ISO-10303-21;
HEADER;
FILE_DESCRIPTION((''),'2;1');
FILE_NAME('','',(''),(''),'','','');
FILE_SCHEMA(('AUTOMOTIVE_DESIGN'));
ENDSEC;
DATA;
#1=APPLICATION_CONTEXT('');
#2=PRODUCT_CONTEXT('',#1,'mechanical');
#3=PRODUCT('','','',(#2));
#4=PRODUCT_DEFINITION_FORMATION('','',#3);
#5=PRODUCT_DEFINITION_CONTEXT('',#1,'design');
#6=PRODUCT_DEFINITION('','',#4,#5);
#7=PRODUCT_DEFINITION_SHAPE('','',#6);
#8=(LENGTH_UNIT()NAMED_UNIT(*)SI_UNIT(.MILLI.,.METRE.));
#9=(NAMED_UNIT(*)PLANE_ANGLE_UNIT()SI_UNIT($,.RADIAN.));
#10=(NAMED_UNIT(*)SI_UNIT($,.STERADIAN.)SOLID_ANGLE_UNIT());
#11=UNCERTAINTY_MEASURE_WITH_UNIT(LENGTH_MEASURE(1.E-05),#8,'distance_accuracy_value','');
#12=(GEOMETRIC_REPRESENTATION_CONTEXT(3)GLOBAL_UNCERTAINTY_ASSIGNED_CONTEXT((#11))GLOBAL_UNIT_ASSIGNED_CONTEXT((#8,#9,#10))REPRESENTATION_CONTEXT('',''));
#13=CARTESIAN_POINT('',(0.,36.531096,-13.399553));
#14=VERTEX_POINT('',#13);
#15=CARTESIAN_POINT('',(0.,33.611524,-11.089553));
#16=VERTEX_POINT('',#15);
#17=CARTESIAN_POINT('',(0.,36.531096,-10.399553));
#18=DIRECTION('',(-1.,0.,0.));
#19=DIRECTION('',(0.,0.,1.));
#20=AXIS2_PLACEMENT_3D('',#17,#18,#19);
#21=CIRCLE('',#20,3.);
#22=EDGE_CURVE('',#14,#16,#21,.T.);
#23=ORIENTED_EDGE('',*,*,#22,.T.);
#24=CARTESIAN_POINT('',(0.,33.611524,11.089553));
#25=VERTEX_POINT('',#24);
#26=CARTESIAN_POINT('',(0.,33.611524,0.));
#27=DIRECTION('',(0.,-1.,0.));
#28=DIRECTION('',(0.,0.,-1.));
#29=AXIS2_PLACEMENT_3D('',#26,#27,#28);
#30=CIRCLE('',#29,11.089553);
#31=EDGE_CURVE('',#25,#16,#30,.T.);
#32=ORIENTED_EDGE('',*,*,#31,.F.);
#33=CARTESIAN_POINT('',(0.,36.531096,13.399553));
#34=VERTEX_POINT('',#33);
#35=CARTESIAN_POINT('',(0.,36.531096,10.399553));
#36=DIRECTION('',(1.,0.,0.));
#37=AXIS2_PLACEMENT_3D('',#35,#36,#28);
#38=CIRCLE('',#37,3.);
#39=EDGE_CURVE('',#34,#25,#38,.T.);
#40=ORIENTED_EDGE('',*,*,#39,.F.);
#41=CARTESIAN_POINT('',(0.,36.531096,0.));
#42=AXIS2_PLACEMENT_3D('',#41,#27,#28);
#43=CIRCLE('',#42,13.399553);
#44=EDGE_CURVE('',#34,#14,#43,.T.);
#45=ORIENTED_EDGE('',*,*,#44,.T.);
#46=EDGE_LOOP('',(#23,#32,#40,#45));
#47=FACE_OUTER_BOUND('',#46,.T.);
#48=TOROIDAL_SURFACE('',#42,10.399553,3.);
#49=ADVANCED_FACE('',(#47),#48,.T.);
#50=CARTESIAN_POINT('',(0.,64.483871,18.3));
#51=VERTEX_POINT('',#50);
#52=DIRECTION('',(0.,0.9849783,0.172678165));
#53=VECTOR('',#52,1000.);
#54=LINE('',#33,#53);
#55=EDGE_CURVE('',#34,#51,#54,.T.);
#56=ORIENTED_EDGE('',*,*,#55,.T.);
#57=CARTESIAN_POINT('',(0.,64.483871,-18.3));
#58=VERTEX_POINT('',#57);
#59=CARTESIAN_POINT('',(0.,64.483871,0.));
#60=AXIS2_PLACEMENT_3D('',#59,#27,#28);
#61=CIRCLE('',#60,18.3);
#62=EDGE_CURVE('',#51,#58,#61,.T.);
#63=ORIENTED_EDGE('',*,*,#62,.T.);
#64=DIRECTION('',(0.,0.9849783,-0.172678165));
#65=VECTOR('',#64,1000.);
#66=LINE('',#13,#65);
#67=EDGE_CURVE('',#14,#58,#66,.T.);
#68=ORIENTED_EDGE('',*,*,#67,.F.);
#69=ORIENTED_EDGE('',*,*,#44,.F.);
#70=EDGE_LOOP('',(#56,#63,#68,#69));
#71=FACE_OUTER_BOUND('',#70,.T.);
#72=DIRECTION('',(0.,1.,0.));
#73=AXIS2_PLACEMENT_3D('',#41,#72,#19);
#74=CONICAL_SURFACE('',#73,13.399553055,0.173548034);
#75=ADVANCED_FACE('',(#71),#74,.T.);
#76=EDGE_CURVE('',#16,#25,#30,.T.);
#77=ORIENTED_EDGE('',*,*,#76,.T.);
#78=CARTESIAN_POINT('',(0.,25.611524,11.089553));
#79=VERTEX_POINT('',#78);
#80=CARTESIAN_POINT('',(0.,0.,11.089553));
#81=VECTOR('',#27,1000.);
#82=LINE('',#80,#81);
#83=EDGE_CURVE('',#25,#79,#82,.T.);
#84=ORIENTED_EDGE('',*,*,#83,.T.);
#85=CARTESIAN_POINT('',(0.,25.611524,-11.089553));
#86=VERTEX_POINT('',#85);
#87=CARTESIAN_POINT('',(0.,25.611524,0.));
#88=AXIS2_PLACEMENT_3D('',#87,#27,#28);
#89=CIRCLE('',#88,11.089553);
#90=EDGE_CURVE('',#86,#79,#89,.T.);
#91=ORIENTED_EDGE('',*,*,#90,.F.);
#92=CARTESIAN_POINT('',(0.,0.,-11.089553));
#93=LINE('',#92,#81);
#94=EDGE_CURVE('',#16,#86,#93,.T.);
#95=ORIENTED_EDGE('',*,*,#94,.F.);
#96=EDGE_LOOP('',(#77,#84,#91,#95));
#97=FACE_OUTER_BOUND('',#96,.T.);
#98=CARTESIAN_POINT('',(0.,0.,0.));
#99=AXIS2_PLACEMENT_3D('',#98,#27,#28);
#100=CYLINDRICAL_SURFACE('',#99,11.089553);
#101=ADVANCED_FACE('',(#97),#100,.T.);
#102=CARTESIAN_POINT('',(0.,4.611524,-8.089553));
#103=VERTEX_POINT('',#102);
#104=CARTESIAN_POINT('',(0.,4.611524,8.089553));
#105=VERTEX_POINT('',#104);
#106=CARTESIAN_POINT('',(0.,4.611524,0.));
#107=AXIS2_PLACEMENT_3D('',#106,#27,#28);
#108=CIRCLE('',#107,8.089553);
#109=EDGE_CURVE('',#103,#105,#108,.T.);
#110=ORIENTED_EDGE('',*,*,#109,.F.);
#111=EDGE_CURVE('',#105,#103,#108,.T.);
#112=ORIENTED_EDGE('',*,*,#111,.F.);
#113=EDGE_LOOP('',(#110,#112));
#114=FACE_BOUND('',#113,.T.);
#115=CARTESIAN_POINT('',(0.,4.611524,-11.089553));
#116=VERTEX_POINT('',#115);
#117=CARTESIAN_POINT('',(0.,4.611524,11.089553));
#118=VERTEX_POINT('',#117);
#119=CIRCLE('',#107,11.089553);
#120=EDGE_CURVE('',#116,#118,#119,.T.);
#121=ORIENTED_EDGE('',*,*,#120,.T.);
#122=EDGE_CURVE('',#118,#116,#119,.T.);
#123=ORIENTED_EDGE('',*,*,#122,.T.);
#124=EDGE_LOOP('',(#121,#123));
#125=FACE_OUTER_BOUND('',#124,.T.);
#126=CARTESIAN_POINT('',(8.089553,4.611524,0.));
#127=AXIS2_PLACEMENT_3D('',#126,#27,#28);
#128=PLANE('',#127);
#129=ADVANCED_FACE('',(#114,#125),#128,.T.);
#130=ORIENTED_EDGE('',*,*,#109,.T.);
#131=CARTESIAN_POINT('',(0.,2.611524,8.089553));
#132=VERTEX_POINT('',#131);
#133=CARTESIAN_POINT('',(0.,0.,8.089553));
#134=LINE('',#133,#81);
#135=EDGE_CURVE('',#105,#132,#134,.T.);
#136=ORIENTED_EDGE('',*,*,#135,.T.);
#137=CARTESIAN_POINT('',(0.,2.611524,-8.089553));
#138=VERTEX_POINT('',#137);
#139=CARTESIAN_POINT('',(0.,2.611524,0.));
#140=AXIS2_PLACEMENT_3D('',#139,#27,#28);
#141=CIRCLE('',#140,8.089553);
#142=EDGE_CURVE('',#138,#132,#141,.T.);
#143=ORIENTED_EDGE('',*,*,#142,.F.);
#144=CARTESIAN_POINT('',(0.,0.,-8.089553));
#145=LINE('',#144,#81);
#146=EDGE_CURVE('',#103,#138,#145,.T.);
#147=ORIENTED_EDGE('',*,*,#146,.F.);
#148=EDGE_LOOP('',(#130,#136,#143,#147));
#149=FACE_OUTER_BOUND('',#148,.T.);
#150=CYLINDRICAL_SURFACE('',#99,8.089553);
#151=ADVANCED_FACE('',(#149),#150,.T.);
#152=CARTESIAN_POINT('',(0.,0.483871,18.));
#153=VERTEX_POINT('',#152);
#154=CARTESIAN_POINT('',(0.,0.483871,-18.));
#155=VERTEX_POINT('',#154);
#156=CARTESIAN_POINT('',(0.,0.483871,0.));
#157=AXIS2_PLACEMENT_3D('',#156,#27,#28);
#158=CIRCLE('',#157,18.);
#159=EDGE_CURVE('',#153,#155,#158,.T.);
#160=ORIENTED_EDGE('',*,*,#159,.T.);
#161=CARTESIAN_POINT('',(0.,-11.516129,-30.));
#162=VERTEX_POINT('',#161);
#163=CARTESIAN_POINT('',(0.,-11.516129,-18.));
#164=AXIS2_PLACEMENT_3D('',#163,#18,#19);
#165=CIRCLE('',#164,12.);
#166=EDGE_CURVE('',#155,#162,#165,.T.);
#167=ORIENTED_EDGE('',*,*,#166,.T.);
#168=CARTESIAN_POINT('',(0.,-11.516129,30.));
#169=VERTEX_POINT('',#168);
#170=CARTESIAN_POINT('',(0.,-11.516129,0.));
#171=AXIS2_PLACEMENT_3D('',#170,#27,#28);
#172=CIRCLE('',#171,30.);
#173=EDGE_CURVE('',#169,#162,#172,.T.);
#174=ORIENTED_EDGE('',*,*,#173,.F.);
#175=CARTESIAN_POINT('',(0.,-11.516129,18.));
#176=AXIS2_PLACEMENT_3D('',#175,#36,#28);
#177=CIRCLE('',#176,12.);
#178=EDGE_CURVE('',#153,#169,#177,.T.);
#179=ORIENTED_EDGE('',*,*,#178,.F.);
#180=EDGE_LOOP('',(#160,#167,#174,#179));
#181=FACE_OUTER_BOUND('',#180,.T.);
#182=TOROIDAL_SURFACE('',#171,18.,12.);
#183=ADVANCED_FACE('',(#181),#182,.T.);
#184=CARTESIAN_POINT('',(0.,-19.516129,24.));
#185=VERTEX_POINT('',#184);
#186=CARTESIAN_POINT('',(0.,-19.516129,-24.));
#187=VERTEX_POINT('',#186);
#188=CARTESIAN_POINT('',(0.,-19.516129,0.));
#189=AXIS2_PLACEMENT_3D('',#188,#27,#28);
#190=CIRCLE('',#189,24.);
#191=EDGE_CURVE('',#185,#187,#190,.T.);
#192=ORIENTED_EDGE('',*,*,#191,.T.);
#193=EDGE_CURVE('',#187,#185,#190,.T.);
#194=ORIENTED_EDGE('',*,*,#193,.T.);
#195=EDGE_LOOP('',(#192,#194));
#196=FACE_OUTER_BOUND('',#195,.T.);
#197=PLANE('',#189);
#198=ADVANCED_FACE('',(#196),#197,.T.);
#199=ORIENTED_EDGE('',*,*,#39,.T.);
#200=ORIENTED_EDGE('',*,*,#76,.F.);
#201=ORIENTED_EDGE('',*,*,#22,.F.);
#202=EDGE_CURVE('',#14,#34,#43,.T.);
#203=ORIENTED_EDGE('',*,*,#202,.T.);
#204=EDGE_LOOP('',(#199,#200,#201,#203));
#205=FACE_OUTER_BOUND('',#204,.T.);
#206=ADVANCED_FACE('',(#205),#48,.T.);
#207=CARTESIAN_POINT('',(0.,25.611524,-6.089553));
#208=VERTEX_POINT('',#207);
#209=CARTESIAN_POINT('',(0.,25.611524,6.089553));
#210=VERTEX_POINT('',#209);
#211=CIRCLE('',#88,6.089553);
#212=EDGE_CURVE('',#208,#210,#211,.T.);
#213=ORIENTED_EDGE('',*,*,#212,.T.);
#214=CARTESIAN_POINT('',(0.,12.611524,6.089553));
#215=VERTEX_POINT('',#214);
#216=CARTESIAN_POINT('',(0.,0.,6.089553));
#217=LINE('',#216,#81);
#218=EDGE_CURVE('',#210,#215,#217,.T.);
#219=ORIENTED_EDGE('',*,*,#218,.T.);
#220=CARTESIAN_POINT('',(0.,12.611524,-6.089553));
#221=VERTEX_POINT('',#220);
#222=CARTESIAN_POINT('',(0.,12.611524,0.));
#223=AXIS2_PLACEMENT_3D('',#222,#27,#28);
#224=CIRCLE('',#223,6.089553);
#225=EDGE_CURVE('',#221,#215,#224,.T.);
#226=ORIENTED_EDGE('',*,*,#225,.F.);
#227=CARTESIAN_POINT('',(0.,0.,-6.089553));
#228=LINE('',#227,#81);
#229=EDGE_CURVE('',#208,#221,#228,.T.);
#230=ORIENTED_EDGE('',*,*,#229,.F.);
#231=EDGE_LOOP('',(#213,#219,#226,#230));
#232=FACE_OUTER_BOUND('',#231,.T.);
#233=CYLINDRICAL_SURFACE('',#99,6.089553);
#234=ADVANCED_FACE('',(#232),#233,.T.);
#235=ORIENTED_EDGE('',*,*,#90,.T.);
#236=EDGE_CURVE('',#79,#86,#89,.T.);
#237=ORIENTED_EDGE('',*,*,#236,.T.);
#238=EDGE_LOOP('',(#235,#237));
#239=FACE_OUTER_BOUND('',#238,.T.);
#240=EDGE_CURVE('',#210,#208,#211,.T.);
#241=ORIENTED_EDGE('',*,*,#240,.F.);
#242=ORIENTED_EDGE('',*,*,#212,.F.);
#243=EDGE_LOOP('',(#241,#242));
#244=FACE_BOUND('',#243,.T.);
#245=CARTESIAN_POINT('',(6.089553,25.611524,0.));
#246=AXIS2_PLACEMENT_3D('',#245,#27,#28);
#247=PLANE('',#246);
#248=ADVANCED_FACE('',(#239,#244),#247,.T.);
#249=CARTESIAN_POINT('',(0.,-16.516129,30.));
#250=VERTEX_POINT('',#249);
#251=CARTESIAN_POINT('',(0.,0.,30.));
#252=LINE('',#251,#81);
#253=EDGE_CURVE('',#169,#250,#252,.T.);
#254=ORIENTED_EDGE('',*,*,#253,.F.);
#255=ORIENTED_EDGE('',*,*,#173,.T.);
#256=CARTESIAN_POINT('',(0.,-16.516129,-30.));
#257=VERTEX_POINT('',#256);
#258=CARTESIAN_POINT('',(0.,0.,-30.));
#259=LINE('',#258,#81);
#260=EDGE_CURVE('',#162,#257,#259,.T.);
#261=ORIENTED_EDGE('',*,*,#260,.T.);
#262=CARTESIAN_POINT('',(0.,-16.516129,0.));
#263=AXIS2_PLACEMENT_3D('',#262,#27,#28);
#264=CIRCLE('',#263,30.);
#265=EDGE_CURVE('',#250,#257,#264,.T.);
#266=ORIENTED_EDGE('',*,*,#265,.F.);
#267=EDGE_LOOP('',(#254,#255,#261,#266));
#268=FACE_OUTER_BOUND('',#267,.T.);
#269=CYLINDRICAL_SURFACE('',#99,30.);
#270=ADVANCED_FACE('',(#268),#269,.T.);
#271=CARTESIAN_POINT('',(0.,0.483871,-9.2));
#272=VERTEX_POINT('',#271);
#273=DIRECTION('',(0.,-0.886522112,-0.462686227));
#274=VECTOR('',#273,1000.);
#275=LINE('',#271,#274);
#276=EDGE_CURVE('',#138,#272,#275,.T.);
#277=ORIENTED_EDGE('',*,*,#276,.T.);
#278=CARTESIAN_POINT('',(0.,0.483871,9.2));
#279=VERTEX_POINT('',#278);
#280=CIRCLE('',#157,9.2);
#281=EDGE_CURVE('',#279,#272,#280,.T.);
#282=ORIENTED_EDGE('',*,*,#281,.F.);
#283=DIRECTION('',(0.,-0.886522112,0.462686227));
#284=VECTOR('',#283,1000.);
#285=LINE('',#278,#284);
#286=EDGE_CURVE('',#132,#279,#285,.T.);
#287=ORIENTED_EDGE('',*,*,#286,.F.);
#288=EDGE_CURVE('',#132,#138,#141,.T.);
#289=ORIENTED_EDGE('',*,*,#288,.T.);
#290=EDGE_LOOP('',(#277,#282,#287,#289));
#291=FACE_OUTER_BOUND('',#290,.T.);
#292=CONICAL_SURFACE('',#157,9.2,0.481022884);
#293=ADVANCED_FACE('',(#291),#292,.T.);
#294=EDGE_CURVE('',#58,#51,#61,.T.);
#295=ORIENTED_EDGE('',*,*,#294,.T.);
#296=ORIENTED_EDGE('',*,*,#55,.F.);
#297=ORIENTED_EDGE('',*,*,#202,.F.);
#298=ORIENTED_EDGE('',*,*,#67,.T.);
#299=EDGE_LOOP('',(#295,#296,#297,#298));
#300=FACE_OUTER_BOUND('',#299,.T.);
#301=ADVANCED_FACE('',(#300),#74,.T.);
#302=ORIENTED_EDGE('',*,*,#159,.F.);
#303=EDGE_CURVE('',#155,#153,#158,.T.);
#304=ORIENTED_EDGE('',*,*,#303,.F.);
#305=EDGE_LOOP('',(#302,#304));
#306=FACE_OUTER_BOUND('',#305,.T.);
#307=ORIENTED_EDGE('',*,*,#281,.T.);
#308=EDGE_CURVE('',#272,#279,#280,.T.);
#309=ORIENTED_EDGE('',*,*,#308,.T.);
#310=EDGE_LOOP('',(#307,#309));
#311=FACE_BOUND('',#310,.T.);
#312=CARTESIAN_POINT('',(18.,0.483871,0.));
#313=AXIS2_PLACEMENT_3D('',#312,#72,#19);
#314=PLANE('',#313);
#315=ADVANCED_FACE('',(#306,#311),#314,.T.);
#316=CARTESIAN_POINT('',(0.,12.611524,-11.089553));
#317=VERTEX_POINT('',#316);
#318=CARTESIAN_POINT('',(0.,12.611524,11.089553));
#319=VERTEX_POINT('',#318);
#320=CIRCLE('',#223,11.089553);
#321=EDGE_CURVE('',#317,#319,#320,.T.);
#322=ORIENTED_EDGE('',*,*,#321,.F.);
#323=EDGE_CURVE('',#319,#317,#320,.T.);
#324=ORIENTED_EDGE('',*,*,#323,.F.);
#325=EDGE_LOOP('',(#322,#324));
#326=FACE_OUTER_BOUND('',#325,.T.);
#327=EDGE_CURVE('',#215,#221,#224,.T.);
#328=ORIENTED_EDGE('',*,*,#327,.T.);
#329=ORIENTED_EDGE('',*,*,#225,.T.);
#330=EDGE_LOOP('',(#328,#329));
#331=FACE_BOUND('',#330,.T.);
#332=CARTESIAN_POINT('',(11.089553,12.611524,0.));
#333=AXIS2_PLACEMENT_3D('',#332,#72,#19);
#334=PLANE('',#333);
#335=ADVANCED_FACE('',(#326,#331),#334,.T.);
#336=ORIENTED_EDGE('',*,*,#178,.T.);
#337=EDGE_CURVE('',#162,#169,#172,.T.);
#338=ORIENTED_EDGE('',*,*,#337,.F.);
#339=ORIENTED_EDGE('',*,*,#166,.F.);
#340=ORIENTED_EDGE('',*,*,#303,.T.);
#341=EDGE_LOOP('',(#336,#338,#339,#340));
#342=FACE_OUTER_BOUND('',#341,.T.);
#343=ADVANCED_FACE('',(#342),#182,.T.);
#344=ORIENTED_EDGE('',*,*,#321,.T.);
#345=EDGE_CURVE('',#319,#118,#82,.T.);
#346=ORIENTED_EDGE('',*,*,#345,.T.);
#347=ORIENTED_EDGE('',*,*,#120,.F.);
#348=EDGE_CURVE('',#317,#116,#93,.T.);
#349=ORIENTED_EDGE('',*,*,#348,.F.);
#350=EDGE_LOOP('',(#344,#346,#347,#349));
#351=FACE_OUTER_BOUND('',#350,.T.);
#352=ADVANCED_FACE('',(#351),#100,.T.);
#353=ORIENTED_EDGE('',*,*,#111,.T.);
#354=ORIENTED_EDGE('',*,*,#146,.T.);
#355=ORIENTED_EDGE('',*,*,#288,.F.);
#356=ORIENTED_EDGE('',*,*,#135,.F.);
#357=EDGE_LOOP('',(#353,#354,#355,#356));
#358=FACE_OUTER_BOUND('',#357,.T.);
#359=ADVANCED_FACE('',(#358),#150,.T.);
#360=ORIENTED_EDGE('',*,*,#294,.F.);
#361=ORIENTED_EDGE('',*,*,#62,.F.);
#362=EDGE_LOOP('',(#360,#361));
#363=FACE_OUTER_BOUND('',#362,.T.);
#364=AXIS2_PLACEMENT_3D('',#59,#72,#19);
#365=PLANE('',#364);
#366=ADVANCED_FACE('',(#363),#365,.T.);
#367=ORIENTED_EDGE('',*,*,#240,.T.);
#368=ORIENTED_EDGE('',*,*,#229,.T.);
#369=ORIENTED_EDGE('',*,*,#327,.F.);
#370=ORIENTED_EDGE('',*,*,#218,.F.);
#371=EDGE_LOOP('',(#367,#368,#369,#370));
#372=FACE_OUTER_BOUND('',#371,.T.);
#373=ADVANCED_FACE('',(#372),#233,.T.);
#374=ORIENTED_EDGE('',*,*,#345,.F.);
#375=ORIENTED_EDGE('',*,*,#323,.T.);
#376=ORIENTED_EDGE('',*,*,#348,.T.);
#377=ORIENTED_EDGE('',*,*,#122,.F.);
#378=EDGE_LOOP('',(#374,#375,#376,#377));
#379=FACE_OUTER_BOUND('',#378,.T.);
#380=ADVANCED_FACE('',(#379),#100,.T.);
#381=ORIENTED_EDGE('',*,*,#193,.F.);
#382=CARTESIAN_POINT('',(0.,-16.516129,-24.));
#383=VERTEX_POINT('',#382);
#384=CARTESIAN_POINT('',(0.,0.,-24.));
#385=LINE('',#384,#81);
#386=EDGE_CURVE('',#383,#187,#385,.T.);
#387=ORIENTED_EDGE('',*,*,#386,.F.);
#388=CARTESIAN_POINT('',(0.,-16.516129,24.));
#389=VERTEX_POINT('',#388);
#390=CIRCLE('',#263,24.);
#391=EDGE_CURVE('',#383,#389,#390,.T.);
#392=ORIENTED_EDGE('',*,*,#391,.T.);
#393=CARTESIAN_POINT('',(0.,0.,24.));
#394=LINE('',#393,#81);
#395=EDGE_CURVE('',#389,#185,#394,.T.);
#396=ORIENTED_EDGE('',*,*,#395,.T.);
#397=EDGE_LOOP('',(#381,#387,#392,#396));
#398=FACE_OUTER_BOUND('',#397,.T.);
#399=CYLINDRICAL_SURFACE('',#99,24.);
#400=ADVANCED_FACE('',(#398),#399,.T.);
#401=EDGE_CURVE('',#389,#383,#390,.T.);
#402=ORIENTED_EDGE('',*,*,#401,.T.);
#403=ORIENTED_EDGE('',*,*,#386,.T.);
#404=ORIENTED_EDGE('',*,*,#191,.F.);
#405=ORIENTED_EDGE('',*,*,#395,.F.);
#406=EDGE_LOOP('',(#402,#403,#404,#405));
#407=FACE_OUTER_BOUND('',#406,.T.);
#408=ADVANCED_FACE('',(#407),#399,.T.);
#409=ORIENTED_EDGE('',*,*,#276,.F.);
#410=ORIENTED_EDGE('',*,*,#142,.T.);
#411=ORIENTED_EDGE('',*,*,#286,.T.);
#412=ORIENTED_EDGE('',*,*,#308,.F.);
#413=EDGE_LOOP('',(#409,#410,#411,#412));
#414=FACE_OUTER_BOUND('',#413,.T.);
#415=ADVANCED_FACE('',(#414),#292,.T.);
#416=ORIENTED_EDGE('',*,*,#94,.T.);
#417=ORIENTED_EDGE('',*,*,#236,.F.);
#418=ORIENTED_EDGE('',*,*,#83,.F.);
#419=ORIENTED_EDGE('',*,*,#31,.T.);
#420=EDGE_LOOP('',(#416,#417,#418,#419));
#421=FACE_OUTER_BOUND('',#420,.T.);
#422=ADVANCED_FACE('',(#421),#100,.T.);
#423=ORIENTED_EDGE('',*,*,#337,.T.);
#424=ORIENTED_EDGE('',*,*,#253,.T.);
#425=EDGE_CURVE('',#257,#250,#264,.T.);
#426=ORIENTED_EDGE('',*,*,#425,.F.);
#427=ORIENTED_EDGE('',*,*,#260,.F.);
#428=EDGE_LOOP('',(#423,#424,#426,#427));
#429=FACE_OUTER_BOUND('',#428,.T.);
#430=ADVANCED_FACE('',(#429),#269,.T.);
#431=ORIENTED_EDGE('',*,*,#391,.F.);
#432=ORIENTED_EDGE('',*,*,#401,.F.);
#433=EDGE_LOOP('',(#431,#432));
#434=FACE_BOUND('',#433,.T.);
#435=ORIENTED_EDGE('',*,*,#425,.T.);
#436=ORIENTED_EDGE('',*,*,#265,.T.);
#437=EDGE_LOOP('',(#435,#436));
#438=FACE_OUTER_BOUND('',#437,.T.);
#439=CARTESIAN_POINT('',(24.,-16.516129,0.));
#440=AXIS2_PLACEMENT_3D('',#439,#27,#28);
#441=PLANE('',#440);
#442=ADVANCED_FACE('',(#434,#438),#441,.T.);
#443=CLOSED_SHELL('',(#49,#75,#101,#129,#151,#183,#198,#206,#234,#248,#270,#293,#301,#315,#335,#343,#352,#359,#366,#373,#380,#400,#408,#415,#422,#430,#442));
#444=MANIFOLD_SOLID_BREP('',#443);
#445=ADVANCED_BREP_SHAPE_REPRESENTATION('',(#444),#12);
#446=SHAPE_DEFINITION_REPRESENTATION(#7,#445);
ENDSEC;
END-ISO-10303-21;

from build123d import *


with BuildPart() as part:
    # 草图1 → 旋转1 (revolve)
    with BuildSketch(Plane.XY, mode=Mode.PRIVATE) as revolve_1_sk:
        with BuildLine():
            Line((0, -19.516129032), (24, -19.516129032))
            Line((24, -19.516129032), (24, -16.516129032))
            Line((24, -16.516129032), (30, -16.516129032))
            Line((30, -16.516129032), (30, -11.516129032))
            ThreePointArc((30, -11.516129032), (26.485281374, -3.030847658), (18, 0.483870968))
            Line((18, 0.483870968), (9.2, 0.483870968))
            Line((9.2, 0.483870968), (8.089553055, 2.611524037))
            Line((8.089553055, 2.611524037), (8.089553055, 4.611524037))
            Line((8.089553055, 4.611524037), (11.089553055, 4.611524037))
            Line((11.089553055, 4.611524037), (11.089553055, 12.611524037))
            Line((11.089553055, 12.611524037), (6.089553055, 12.611524037))
            Line((6.089553055, 12.611524037), (6.089553055, 25.611524037))
            Line((6.089553055, 25.611524037), (11.089553055, 25.611524037))
            Line((11.089553055, 25.611524037), (11.089553055, 33.611524037))
            ThreePointArc((11.089553055, 33.611524037), (12.752211126, 34.669644876), (13.399553055, 36.531095923))
            Line((13.399553055, 36.531095923), (18.3, 64.483870968))
            Line((18.3, 64.483870968), (0, 64.483870968))
            Line((0, 64.483870968), (0, -19.516129032))
        make_face()
    revolve(revolve_1_sk.sketch.rotate(Axis((0, 0, 0), (0, 1, 0)), 90), axis=Axis((0, 0, 0), (0, 1, 0)))


solid = part.part
